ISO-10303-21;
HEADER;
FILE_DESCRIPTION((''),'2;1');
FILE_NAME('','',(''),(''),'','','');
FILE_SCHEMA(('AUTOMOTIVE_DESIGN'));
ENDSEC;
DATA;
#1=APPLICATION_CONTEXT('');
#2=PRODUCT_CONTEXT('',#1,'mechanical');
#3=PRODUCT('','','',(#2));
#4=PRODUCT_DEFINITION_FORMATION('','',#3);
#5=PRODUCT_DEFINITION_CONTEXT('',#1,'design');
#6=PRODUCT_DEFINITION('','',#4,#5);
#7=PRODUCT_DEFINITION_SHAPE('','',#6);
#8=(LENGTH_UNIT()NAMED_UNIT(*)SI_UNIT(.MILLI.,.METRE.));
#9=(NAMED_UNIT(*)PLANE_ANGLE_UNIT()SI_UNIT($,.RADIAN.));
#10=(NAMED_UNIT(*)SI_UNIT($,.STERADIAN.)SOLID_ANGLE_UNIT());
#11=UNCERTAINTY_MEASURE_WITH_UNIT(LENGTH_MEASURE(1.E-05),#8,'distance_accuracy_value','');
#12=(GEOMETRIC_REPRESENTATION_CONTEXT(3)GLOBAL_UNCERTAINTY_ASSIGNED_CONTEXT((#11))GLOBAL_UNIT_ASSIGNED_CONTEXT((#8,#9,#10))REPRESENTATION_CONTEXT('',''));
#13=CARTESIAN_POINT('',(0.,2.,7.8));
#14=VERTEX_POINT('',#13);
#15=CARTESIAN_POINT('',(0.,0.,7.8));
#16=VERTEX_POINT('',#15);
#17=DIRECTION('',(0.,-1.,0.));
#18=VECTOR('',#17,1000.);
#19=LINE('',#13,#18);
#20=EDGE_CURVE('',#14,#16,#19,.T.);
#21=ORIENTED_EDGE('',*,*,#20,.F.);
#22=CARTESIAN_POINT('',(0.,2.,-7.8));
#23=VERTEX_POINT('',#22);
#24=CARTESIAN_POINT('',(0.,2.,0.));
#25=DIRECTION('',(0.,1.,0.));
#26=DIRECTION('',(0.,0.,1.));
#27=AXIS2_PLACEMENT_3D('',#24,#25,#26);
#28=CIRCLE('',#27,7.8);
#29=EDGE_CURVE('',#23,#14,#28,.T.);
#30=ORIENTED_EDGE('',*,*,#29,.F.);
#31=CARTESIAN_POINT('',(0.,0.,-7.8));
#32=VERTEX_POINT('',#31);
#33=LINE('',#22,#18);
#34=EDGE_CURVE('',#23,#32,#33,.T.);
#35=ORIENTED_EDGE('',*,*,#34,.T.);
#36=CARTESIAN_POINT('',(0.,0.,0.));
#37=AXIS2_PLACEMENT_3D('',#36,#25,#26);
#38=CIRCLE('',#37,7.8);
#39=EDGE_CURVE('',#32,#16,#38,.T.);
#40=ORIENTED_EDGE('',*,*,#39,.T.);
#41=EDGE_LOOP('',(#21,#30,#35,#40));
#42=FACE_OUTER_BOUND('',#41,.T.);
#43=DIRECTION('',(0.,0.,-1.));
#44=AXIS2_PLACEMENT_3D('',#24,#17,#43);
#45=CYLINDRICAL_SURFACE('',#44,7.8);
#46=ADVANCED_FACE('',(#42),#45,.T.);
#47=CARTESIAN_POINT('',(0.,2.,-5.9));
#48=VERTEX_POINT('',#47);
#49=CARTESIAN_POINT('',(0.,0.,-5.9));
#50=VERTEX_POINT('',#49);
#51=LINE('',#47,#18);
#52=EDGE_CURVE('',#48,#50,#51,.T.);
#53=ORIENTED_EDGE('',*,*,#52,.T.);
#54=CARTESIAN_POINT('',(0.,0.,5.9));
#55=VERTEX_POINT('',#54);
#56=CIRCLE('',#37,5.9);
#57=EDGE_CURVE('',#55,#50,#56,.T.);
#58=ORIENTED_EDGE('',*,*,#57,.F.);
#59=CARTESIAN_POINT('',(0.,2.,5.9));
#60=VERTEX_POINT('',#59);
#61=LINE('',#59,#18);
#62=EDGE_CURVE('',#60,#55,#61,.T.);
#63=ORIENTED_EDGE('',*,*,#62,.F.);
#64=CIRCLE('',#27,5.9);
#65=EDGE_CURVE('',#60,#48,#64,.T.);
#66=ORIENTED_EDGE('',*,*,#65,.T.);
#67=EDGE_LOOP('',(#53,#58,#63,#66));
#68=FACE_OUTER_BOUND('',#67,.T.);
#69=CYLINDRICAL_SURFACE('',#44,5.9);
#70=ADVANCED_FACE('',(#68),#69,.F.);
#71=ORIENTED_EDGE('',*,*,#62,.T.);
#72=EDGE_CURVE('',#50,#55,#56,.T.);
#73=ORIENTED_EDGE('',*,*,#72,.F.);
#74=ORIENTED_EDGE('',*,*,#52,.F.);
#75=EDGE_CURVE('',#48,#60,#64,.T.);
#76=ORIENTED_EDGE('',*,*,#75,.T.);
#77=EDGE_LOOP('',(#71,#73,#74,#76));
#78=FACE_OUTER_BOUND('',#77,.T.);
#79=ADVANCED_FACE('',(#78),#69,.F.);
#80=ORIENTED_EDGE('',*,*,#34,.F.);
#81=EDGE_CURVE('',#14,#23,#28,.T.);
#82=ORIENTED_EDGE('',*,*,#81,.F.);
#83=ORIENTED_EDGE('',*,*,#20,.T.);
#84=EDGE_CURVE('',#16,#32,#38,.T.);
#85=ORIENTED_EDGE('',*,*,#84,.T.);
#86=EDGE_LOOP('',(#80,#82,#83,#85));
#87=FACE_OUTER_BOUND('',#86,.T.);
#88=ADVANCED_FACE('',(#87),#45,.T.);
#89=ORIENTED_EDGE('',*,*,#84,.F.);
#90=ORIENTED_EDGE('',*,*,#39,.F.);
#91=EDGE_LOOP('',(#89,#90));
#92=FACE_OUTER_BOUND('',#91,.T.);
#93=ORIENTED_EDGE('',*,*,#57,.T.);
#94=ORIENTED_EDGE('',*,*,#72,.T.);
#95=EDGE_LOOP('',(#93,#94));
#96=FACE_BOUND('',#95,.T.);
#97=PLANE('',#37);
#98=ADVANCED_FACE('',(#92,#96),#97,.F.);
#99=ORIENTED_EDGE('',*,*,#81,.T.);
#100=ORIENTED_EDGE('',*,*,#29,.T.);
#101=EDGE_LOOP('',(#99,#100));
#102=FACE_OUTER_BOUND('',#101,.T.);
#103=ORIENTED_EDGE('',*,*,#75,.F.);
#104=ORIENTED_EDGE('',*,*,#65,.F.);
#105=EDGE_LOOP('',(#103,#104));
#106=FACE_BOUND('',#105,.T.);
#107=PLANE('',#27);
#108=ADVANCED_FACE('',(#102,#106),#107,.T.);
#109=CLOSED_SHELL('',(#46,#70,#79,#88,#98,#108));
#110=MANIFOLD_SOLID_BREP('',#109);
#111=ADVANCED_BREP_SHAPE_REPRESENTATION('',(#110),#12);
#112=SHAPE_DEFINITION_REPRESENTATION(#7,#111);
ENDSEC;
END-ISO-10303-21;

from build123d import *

# Parameters (mm, degrees)
SKETCH1_R           = 7.8
SKETCH1_R_2         = 5.9
BOSS_EXTRUDE1_DEPTH = 2


with BuildPart() as part:
    # Sketch1 → Boss-Extrude1 (new body)
    with BuildSketch(Plane(origin=(0, 0, 0), x_dir=(1, 0, 0), z_dir=(0, 1, 0))):
        with Locations(Location((0, 0, 0), (0, 0, 270))):
            Circle(SKETCH1_R)
        with Locations(Location((0, 0, 0), (0, 0, 270))):
            Circle(SKETCH1_R_2, mode=Mode.SUBTRACT)
    extrude(amount=BOSS_EXTRUDE1_DEPTH)


solid = part.part
